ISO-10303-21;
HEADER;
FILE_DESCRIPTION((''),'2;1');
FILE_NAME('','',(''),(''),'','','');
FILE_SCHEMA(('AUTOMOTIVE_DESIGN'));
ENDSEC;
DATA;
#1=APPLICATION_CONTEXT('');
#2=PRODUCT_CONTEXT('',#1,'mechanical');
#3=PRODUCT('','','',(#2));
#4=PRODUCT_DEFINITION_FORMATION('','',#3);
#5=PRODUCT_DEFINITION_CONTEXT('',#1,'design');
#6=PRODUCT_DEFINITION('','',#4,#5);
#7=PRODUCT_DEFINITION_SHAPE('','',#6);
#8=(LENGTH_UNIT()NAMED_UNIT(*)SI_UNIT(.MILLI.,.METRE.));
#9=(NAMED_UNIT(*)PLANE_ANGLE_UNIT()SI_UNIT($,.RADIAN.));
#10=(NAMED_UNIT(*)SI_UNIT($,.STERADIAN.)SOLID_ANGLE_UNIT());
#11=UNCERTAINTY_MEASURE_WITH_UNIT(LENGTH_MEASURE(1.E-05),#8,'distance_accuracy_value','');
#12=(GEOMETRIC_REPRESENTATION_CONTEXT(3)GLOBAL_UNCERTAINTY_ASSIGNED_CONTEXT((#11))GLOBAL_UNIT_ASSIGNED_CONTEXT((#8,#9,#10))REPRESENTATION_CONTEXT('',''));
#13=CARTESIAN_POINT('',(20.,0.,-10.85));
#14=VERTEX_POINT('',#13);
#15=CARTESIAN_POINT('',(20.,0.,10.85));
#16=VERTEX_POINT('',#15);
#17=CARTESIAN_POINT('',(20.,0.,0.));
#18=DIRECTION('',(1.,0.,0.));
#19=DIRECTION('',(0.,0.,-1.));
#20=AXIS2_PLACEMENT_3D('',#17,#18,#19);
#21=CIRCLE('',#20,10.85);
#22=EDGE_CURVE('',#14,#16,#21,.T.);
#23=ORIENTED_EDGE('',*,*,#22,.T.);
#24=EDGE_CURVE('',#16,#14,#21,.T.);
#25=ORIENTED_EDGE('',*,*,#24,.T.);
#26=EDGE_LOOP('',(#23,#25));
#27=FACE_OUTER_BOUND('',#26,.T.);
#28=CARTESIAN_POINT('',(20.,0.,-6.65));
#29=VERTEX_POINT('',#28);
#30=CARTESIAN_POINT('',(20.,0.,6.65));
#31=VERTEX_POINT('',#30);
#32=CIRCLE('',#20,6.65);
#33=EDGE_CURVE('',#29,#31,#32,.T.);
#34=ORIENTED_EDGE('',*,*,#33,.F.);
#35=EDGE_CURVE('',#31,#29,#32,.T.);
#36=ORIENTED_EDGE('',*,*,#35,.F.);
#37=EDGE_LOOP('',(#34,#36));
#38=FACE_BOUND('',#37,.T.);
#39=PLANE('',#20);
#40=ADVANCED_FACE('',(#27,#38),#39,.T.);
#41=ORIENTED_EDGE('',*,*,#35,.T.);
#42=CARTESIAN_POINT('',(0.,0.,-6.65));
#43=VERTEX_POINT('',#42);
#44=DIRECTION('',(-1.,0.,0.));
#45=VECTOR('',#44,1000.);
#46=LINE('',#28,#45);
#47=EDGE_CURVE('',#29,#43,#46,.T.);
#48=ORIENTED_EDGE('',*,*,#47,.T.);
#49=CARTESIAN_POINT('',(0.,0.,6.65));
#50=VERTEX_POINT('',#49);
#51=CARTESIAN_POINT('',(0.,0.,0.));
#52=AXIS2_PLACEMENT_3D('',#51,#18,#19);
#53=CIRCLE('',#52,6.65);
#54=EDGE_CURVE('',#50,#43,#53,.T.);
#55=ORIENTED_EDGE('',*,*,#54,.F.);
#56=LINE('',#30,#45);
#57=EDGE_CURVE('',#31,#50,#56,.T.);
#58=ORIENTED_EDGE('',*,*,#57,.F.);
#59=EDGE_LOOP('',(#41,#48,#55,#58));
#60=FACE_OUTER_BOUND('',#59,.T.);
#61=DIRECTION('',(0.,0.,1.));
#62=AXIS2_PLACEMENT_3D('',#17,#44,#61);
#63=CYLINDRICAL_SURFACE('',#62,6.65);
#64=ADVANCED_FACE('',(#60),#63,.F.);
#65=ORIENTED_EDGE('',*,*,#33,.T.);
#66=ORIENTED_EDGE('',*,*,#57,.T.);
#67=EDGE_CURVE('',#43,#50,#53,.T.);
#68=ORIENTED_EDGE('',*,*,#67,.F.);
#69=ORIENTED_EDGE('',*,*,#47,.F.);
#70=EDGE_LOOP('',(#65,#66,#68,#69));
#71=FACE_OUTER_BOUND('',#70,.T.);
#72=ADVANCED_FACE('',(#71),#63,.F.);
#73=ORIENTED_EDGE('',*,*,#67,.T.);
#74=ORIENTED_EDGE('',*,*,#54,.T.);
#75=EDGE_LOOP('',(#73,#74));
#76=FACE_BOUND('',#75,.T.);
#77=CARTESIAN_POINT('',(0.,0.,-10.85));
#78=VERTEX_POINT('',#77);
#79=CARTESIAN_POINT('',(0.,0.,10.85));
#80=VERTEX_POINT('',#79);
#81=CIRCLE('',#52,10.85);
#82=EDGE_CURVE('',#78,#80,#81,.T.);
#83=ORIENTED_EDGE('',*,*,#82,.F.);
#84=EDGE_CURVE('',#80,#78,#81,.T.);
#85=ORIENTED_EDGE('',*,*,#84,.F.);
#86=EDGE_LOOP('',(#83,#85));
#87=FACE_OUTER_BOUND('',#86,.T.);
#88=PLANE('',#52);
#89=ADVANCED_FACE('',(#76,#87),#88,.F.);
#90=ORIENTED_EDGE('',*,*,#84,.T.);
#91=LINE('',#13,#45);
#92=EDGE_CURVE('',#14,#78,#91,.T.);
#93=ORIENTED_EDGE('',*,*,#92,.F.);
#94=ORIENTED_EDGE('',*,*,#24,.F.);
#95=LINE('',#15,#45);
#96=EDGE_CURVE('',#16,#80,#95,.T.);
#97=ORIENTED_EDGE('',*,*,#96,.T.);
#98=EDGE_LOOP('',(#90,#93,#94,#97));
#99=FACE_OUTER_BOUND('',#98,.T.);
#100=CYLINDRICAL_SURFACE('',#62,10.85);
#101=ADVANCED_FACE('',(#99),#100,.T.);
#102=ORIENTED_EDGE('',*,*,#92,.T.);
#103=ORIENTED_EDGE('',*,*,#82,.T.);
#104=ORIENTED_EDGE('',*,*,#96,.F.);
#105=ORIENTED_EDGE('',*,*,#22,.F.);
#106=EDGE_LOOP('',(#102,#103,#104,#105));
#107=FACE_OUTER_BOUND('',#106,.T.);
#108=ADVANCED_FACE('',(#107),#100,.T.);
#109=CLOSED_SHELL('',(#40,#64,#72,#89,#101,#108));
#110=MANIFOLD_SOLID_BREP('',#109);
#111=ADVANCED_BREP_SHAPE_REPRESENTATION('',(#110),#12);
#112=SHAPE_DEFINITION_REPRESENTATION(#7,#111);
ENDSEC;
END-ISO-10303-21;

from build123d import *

# Parameters (mm, degrees)
SKETCH1_R           = 10.85
SKETCH1_R_2         = 6.65
BOSS_EXTRUDE1_DEPTH = 20


with BuildPart() as part:
    # Sketch1 → Boss-Extrude1 (new body)
    with BuildSketch(Plane(origin=(0, 0, 0), x_dir=(0, 0, -1), z_dir=(1, 0, 0))):
        Circle(SKETCH1_R)
        Circle(SKETCH1_R_2, mode=Mode.SUBTRACT)
    extrude(amount=BOSS_EXTRUDE1_DEPTH)


solid = part.part
